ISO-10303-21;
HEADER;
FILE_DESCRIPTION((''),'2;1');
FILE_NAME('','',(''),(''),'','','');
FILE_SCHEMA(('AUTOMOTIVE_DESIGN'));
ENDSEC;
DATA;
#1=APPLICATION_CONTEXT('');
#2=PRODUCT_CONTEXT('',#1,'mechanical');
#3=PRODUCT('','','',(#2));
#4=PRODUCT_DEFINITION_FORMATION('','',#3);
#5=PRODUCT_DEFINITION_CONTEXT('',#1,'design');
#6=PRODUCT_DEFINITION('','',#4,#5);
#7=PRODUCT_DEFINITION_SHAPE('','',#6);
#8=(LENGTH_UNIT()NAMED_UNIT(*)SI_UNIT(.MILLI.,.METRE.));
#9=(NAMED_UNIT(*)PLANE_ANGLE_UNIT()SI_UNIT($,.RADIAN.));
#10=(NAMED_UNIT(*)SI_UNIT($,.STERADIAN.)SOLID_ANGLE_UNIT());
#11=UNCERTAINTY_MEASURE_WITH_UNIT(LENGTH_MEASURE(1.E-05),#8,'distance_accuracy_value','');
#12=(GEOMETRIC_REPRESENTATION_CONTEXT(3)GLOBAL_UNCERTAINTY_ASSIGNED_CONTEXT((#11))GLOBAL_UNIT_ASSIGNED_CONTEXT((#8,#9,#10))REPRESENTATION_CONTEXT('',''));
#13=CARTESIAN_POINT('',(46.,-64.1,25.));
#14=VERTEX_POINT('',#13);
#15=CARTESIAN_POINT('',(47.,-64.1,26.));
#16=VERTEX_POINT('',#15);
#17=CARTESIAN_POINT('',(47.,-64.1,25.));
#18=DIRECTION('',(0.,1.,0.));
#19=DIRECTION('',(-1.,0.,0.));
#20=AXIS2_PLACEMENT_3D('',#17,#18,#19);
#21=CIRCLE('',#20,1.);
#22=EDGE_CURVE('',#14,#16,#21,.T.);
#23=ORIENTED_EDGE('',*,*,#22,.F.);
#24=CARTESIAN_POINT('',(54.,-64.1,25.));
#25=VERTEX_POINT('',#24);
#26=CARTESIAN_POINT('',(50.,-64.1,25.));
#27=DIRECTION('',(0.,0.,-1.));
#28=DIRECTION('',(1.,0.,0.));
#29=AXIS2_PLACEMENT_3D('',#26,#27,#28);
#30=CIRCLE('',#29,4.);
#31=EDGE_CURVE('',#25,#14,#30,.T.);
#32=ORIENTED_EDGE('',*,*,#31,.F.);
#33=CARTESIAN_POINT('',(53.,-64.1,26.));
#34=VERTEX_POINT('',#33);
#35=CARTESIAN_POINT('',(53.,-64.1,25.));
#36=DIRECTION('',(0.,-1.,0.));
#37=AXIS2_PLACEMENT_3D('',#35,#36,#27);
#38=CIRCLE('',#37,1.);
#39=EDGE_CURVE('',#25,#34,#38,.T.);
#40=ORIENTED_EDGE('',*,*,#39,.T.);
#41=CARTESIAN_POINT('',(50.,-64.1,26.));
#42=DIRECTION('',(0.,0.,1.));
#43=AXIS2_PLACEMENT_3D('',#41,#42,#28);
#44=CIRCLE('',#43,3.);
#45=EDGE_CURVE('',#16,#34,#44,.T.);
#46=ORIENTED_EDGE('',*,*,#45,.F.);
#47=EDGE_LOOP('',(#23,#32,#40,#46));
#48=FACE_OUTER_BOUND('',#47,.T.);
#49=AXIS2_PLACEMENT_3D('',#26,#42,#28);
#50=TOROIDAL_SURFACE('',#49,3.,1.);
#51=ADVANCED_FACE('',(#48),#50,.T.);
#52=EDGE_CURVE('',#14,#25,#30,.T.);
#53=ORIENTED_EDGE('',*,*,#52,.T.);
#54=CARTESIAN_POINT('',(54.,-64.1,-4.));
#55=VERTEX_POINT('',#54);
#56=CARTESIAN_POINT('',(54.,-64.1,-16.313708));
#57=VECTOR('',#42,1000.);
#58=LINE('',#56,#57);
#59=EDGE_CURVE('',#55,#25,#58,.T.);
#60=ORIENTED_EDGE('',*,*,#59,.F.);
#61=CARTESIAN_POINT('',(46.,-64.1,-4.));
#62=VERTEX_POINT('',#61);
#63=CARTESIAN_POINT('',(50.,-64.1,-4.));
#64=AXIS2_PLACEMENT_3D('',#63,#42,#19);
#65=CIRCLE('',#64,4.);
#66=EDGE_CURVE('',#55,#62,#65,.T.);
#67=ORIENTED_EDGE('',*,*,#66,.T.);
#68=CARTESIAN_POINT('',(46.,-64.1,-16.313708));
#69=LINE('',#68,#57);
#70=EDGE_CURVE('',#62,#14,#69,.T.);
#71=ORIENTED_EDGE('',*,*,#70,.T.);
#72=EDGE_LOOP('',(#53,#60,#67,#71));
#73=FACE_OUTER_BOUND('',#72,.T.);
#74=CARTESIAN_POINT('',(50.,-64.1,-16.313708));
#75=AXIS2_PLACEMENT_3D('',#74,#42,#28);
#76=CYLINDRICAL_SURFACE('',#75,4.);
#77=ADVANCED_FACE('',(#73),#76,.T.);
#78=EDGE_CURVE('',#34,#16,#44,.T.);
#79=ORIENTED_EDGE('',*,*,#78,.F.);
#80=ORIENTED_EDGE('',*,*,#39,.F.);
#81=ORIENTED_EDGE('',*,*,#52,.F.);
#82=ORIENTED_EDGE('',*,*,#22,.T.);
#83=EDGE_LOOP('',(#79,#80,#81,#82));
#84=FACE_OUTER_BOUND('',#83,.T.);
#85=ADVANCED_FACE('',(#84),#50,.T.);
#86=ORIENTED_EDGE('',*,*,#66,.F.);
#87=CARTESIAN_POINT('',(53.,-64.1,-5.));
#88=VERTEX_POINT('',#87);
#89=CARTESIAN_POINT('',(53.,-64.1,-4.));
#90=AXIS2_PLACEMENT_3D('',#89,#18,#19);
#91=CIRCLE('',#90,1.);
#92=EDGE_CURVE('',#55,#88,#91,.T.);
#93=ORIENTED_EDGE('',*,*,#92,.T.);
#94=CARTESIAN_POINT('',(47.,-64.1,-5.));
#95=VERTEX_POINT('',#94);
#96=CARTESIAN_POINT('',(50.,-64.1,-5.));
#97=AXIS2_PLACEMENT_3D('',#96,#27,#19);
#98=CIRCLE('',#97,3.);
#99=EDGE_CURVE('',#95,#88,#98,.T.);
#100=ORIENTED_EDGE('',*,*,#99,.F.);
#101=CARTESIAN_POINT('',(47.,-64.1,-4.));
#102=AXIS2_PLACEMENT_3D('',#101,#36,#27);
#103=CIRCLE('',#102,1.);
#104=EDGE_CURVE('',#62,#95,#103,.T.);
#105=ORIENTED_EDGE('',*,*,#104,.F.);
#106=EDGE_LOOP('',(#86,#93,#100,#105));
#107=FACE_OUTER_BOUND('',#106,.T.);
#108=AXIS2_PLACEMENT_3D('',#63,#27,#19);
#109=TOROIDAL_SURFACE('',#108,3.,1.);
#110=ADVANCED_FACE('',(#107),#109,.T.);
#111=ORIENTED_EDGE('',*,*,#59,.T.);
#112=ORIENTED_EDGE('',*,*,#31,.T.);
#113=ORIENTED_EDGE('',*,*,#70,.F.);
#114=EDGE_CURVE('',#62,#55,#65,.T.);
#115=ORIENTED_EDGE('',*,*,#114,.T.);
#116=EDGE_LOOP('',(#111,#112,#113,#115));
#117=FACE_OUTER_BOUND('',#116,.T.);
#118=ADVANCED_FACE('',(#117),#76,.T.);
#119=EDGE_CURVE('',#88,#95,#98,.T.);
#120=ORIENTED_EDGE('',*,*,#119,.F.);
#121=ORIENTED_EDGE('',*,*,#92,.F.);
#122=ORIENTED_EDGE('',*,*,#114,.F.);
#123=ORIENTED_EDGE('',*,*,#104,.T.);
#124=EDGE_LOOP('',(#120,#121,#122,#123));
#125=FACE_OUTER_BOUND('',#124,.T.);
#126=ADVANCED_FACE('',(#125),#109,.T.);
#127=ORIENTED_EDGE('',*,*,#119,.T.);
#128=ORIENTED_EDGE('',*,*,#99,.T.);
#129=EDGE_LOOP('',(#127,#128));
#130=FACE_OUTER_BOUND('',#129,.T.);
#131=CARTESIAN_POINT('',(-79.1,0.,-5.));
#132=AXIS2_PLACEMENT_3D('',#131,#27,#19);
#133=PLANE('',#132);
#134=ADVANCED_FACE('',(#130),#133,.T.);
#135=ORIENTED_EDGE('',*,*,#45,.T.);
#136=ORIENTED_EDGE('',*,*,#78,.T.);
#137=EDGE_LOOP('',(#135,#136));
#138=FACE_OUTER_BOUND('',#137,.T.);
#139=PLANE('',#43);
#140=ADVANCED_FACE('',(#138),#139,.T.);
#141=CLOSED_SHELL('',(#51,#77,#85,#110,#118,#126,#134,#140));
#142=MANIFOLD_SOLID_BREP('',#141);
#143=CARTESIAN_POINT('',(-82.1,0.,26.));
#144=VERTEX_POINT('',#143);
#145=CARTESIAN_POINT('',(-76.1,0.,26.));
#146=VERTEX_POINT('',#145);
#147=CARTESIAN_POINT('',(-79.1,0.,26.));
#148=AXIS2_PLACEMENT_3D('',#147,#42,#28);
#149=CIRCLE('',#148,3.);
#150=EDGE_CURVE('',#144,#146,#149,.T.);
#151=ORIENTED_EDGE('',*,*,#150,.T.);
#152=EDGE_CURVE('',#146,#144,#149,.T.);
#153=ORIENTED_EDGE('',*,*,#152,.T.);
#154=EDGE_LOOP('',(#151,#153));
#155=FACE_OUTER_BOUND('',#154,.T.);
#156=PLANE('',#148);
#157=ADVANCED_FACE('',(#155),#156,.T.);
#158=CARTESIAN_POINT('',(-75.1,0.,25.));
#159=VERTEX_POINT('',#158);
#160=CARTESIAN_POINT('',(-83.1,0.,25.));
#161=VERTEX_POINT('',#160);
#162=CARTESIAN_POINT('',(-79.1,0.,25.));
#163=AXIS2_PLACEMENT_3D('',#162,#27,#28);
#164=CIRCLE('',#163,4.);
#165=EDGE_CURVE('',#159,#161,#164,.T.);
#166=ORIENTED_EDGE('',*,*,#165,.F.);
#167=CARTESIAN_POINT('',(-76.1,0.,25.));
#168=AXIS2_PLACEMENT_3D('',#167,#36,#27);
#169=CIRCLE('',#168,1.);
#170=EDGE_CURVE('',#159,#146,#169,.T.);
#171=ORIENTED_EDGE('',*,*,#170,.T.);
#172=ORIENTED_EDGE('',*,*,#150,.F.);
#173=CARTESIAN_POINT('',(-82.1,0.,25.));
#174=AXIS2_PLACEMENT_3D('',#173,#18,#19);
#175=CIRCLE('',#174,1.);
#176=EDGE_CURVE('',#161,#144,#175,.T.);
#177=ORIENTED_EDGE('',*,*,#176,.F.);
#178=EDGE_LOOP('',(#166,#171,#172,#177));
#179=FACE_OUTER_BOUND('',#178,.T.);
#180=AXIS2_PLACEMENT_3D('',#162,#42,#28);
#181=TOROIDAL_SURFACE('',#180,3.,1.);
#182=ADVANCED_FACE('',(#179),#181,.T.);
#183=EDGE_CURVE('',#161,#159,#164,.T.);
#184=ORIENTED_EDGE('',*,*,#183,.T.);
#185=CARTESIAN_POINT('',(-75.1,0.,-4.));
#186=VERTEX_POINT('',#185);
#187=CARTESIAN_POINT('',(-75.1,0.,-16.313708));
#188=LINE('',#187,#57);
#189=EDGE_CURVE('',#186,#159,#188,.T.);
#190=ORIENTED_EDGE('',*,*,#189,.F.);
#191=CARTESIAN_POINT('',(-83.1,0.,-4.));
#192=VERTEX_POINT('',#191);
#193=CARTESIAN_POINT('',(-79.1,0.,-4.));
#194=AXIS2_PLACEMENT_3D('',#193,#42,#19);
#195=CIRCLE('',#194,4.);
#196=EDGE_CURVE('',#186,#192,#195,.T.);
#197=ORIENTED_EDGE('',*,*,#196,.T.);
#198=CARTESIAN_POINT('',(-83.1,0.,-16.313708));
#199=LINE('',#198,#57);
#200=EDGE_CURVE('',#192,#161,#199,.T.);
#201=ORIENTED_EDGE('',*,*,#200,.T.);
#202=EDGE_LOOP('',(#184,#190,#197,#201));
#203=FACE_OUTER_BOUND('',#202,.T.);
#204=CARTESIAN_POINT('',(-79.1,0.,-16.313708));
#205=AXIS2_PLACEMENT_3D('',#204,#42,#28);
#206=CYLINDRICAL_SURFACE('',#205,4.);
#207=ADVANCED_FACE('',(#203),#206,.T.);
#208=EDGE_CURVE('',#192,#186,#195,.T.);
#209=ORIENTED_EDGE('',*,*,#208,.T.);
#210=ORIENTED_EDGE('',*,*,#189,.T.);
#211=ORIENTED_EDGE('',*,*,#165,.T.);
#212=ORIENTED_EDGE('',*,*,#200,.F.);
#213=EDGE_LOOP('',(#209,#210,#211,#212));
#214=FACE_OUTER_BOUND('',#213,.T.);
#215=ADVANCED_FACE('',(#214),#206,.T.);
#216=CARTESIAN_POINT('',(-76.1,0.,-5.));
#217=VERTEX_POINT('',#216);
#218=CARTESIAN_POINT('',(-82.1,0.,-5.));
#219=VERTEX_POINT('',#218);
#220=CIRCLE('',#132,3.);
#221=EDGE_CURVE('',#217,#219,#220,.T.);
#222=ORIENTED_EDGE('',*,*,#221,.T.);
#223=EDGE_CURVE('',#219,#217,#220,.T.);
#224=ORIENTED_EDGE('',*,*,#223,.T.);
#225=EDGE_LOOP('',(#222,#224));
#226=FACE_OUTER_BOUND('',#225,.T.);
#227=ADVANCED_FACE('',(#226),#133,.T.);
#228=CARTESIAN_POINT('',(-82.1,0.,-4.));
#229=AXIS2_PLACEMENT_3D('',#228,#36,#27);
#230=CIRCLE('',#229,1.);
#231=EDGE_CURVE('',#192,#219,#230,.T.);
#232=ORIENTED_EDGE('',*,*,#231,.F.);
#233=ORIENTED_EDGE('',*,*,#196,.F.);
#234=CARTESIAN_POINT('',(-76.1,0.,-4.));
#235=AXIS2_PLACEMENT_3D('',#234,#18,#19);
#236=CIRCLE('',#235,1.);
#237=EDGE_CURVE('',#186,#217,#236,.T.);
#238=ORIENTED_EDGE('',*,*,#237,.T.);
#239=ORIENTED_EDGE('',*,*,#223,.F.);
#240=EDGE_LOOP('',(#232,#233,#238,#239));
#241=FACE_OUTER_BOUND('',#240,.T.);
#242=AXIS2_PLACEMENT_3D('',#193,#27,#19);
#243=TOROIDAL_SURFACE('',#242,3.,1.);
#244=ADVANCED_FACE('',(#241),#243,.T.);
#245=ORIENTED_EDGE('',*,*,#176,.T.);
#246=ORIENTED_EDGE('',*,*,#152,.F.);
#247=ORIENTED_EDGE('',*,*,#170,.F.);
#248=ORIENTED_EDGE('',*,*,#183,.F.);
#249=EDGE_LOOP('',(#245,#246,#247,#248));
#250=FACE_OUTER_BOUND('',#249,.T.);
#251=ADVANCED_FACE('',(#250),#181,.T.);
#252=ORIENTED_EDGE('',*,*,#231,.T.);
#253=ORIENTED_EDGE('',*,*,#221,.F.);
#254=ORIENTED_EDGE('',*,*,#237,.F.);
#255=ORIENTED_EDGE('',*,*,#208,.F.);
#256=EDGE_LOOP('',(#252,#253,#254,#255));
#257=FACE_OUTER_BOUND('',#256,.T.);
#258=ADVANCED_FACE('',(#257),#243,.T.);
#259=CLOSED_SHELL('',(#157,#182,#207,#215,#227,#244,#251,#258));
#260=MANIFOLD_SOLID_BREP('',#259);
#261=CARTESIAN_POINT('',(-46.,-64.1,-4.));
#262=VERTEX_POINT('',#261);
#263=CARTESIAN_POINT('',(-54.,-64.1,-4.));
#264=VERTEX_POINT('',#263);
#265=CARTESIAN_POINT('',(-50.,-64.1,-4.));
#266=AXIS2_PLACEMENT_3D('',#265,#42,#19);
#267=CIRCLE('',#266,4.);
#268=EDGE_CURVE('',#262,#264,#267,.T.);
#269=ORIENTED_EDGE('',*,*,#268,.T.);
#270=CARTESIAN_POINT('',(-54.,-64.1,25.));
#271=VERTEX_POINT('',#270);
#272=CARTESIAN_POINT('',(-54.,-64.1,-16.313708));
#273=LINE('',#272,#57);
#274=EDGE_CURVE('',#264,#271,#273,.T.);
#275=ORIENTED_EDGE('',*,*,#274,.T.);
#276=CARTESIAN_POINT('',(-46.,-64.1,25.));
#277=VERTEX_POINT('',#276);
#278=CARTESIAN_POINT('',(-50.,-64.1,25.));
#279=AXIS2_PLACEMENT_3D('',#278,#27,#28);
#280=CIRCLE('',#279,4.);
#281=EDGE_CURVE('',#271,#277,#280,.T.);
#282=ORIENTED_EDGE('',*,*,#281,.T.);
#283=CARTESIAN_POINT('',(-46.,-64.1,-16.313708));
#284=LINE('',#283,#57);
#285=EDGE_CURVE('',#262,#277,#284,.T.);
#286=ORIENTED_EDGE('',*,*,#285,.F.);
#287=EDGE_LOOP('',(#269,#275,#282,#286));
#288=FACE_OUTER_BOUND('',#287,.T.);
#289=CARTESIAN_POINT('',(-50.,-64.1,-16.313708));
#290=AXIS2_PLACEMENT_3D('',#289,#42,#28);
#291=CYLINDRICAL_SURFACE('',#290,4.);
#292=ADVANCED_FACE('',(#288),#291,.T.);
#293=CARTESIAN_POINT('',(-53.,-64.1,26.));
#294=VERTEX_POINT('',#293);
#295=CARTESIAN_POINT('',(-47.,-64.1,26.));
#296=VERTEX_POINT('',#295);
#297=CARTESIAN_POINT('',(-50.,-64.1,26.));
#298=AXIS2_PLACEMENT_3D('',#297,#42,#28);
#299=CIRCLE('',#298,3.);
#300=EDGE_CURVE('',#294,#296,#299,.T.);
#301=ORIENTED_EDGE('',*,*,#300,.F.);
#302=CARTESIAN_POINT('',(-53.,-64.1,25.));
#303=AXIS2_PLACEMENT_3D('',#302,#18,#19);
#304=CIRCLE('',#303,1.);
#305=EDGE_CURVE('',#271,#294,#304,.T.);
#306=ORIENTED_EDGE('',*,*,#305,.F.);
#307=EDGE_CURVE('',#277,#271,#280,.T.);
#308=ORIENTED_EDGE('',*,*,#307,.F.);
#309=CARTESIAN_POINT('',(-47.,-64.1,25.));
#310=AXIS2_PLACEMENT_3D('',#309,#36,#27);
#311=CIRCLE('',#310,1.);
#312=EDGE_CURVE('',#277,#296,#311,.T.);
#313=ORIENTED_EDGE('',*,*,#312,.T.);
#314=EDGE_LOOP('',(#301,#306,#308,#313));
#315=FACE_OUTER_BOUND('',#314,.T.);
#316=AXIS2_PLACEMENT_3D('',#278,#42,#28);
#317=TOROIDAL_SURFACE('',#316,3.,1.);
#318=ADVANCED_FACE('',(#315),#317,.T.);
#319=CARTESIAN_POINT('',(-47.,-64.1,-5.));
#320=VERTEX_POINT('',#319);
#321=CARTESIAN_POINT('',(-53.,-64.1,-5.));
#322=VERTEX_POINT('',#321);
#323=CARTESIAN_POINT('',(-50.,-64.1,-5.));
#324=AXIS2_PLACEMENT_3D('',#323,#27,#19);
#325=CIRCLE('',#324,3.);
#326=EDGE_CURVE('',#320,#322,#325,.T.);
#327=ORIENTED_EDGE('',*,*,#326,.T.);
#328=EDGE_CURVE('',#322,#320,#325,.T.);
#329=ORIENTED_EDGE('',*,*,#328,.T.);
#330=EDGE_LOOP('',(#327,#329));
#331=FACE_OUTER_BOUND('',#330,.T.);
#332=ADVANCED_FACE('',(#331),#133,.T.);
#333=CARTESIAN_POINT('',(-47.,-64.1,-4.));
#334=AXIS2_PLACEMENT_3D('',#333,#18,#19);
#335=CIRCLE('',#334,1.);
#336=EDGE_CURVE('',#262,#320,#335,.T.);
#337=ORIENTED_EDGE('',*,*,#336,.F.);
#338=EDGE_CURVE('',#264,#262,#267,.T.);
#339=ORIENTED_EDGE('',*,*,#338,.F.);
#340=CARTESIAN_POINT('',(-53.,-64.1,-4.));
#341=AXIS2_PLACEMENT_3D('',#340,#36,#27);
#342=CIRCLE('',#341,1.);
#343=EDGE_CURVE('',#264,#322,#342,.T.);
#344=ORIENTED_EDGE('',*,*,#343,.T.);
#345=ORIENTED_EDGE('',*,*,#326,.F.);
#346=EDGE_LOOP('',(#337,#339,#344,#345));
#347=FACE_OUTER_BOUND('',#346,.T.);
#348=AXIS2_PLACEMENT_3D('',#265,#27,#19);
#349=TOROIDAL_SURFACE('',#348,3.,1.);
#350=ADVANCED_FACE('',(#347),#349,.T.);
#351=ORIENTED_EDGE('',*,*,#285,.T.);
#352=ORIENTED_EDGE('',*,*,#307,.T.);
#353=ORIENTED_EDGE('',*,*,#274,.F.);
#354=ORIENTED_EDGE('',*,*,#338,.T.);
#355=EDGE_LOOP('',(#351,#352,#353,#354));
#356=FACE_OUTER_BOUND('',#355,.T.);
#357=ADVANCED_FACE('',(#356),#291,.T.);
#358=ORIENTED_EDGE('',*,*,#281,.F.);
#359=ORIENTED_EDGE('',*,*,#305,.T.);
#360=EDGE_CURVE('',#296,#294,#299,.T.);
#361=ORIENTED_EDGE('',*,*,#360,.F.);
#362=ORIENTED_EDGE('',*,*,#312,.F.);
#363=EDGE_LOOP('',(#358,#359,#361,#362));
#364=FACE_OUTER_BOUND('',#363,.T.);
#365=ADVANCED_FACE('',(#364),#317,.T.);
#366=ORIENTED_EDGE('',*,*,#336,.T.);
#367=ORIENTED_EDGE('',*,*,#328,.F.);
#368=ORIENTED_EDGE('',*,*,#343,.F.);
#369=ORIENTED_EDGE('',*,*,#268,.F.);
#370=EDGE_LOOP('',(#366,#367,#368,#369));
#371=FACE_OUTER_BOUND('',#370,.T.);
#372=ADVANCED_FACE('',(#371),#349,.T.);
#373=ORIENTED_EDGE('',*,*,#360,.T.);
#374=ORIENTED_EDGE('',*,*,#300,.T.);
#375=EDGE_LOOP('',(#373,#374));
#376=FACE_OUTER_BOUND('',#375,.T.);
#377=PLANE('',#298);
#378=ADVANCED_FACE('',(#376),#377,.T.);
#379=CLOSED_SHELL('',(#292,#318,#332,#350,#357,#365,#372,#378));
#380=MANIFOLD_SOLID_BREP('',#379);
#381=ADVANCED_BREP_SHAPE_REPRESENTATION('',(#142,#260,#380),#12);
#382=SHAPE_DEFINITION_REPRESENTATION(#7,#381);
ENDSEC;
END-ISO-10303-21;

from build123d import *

# Parameters (mm, degrees)
BOSS_EXTRUDE1_DEPTH        = 26
BOSS_EXTRUDE1_DEPTH_BACK   = 5
SKETCH1_R                  = 4
BOSS_EXTRUDE1_2_DEPTH      = 26
BOSS_EXTRUDE1_2_DEPTH_BACK = 5
BOSS_EXTRUDE1_3_DEPTH      = 26
BOSS_EXTRUDE1_3_DEPTH_BACK = 5
FILLET1_R                  = 1
FILLET2_R                  = 1
FILLET3_R                  = 1


with BuildPart() as part:
    # Sketch1 → Boss-Extrude1 (new, two sides: drawn at the far end of the back side and taken through both)
    with BuildSketch(Plane.XY.offset(-BOSS_EXTRUDE1_DEPTH_BACK)):
        with Locations((-79.1, 0)):
            Circle(SKETCH1_R)
    extrude(amount=BOSS_EXTRUDE1_DEPTH + BOSS_EXTRUDE1_DEPTH_BACK)

    # Fillet1
    fillet1_edges = [part.edges().sort_by_distance(p)[0] for p in [
        (-83.1, 0, -5),
        (-83.1, 0, 26),
    ]]
    fillet(fillet1_edges, radius=FILLET1_R)


with BuildPart() as body_2:
    # Sketch1 → Boss-Extrude1 2 (new, two sides: drawn at the far end of the back side and taken through both)
    with BuildSketch(Plane.XY.offset(-BOSS_EXTRUDE1_2_DEPTH_BACK)):
        with Locations((-50, -64.1)):
            Circle(SKETCH1_R)
    extrude(amount=BOSS_EXTRUDE1_2_DEPTH + BOSS_EXTRUDE1_2_DEPTH_BACK)

    # Fillet2
    fillet2_edges = [body_2.edges().sort_by_distance(p)[0] for p in [
        (-54, -64.1, 26),
        (-54, -64.1, -5),
    ]]
    fillet(fillet2_edges, radius=FILLET2_R)


with BuildPart() as body_3:
    # Sketch1 → Boss-Extrude1 3 (new, two sides: drawn at the far end of the back side and taken through both)
    with BuildSketch(Plane.XY.offset(-BOSS_EXTRUDE1_3_DEPTH_BACK)):
        with Locations((50, -64.1)):
            Circle(SKETCH1_R)
    extrude(amount=BOSS_EXTRUDE1_3_DEPTH + BOSS_EXTRUDE1_3_DEPTH_BACK)

    # Fillet3
    fillet3_edges = [body_3.edges().sort_by_distance(p)[0] for p in [
        (46, -64.1, 26),
        (46, -64.1, -5),
    ]]
    fillet(fillet3_edges, radius=FILLET3_R)


solid = Compound([part.part, body_2.part, body_3.part])
